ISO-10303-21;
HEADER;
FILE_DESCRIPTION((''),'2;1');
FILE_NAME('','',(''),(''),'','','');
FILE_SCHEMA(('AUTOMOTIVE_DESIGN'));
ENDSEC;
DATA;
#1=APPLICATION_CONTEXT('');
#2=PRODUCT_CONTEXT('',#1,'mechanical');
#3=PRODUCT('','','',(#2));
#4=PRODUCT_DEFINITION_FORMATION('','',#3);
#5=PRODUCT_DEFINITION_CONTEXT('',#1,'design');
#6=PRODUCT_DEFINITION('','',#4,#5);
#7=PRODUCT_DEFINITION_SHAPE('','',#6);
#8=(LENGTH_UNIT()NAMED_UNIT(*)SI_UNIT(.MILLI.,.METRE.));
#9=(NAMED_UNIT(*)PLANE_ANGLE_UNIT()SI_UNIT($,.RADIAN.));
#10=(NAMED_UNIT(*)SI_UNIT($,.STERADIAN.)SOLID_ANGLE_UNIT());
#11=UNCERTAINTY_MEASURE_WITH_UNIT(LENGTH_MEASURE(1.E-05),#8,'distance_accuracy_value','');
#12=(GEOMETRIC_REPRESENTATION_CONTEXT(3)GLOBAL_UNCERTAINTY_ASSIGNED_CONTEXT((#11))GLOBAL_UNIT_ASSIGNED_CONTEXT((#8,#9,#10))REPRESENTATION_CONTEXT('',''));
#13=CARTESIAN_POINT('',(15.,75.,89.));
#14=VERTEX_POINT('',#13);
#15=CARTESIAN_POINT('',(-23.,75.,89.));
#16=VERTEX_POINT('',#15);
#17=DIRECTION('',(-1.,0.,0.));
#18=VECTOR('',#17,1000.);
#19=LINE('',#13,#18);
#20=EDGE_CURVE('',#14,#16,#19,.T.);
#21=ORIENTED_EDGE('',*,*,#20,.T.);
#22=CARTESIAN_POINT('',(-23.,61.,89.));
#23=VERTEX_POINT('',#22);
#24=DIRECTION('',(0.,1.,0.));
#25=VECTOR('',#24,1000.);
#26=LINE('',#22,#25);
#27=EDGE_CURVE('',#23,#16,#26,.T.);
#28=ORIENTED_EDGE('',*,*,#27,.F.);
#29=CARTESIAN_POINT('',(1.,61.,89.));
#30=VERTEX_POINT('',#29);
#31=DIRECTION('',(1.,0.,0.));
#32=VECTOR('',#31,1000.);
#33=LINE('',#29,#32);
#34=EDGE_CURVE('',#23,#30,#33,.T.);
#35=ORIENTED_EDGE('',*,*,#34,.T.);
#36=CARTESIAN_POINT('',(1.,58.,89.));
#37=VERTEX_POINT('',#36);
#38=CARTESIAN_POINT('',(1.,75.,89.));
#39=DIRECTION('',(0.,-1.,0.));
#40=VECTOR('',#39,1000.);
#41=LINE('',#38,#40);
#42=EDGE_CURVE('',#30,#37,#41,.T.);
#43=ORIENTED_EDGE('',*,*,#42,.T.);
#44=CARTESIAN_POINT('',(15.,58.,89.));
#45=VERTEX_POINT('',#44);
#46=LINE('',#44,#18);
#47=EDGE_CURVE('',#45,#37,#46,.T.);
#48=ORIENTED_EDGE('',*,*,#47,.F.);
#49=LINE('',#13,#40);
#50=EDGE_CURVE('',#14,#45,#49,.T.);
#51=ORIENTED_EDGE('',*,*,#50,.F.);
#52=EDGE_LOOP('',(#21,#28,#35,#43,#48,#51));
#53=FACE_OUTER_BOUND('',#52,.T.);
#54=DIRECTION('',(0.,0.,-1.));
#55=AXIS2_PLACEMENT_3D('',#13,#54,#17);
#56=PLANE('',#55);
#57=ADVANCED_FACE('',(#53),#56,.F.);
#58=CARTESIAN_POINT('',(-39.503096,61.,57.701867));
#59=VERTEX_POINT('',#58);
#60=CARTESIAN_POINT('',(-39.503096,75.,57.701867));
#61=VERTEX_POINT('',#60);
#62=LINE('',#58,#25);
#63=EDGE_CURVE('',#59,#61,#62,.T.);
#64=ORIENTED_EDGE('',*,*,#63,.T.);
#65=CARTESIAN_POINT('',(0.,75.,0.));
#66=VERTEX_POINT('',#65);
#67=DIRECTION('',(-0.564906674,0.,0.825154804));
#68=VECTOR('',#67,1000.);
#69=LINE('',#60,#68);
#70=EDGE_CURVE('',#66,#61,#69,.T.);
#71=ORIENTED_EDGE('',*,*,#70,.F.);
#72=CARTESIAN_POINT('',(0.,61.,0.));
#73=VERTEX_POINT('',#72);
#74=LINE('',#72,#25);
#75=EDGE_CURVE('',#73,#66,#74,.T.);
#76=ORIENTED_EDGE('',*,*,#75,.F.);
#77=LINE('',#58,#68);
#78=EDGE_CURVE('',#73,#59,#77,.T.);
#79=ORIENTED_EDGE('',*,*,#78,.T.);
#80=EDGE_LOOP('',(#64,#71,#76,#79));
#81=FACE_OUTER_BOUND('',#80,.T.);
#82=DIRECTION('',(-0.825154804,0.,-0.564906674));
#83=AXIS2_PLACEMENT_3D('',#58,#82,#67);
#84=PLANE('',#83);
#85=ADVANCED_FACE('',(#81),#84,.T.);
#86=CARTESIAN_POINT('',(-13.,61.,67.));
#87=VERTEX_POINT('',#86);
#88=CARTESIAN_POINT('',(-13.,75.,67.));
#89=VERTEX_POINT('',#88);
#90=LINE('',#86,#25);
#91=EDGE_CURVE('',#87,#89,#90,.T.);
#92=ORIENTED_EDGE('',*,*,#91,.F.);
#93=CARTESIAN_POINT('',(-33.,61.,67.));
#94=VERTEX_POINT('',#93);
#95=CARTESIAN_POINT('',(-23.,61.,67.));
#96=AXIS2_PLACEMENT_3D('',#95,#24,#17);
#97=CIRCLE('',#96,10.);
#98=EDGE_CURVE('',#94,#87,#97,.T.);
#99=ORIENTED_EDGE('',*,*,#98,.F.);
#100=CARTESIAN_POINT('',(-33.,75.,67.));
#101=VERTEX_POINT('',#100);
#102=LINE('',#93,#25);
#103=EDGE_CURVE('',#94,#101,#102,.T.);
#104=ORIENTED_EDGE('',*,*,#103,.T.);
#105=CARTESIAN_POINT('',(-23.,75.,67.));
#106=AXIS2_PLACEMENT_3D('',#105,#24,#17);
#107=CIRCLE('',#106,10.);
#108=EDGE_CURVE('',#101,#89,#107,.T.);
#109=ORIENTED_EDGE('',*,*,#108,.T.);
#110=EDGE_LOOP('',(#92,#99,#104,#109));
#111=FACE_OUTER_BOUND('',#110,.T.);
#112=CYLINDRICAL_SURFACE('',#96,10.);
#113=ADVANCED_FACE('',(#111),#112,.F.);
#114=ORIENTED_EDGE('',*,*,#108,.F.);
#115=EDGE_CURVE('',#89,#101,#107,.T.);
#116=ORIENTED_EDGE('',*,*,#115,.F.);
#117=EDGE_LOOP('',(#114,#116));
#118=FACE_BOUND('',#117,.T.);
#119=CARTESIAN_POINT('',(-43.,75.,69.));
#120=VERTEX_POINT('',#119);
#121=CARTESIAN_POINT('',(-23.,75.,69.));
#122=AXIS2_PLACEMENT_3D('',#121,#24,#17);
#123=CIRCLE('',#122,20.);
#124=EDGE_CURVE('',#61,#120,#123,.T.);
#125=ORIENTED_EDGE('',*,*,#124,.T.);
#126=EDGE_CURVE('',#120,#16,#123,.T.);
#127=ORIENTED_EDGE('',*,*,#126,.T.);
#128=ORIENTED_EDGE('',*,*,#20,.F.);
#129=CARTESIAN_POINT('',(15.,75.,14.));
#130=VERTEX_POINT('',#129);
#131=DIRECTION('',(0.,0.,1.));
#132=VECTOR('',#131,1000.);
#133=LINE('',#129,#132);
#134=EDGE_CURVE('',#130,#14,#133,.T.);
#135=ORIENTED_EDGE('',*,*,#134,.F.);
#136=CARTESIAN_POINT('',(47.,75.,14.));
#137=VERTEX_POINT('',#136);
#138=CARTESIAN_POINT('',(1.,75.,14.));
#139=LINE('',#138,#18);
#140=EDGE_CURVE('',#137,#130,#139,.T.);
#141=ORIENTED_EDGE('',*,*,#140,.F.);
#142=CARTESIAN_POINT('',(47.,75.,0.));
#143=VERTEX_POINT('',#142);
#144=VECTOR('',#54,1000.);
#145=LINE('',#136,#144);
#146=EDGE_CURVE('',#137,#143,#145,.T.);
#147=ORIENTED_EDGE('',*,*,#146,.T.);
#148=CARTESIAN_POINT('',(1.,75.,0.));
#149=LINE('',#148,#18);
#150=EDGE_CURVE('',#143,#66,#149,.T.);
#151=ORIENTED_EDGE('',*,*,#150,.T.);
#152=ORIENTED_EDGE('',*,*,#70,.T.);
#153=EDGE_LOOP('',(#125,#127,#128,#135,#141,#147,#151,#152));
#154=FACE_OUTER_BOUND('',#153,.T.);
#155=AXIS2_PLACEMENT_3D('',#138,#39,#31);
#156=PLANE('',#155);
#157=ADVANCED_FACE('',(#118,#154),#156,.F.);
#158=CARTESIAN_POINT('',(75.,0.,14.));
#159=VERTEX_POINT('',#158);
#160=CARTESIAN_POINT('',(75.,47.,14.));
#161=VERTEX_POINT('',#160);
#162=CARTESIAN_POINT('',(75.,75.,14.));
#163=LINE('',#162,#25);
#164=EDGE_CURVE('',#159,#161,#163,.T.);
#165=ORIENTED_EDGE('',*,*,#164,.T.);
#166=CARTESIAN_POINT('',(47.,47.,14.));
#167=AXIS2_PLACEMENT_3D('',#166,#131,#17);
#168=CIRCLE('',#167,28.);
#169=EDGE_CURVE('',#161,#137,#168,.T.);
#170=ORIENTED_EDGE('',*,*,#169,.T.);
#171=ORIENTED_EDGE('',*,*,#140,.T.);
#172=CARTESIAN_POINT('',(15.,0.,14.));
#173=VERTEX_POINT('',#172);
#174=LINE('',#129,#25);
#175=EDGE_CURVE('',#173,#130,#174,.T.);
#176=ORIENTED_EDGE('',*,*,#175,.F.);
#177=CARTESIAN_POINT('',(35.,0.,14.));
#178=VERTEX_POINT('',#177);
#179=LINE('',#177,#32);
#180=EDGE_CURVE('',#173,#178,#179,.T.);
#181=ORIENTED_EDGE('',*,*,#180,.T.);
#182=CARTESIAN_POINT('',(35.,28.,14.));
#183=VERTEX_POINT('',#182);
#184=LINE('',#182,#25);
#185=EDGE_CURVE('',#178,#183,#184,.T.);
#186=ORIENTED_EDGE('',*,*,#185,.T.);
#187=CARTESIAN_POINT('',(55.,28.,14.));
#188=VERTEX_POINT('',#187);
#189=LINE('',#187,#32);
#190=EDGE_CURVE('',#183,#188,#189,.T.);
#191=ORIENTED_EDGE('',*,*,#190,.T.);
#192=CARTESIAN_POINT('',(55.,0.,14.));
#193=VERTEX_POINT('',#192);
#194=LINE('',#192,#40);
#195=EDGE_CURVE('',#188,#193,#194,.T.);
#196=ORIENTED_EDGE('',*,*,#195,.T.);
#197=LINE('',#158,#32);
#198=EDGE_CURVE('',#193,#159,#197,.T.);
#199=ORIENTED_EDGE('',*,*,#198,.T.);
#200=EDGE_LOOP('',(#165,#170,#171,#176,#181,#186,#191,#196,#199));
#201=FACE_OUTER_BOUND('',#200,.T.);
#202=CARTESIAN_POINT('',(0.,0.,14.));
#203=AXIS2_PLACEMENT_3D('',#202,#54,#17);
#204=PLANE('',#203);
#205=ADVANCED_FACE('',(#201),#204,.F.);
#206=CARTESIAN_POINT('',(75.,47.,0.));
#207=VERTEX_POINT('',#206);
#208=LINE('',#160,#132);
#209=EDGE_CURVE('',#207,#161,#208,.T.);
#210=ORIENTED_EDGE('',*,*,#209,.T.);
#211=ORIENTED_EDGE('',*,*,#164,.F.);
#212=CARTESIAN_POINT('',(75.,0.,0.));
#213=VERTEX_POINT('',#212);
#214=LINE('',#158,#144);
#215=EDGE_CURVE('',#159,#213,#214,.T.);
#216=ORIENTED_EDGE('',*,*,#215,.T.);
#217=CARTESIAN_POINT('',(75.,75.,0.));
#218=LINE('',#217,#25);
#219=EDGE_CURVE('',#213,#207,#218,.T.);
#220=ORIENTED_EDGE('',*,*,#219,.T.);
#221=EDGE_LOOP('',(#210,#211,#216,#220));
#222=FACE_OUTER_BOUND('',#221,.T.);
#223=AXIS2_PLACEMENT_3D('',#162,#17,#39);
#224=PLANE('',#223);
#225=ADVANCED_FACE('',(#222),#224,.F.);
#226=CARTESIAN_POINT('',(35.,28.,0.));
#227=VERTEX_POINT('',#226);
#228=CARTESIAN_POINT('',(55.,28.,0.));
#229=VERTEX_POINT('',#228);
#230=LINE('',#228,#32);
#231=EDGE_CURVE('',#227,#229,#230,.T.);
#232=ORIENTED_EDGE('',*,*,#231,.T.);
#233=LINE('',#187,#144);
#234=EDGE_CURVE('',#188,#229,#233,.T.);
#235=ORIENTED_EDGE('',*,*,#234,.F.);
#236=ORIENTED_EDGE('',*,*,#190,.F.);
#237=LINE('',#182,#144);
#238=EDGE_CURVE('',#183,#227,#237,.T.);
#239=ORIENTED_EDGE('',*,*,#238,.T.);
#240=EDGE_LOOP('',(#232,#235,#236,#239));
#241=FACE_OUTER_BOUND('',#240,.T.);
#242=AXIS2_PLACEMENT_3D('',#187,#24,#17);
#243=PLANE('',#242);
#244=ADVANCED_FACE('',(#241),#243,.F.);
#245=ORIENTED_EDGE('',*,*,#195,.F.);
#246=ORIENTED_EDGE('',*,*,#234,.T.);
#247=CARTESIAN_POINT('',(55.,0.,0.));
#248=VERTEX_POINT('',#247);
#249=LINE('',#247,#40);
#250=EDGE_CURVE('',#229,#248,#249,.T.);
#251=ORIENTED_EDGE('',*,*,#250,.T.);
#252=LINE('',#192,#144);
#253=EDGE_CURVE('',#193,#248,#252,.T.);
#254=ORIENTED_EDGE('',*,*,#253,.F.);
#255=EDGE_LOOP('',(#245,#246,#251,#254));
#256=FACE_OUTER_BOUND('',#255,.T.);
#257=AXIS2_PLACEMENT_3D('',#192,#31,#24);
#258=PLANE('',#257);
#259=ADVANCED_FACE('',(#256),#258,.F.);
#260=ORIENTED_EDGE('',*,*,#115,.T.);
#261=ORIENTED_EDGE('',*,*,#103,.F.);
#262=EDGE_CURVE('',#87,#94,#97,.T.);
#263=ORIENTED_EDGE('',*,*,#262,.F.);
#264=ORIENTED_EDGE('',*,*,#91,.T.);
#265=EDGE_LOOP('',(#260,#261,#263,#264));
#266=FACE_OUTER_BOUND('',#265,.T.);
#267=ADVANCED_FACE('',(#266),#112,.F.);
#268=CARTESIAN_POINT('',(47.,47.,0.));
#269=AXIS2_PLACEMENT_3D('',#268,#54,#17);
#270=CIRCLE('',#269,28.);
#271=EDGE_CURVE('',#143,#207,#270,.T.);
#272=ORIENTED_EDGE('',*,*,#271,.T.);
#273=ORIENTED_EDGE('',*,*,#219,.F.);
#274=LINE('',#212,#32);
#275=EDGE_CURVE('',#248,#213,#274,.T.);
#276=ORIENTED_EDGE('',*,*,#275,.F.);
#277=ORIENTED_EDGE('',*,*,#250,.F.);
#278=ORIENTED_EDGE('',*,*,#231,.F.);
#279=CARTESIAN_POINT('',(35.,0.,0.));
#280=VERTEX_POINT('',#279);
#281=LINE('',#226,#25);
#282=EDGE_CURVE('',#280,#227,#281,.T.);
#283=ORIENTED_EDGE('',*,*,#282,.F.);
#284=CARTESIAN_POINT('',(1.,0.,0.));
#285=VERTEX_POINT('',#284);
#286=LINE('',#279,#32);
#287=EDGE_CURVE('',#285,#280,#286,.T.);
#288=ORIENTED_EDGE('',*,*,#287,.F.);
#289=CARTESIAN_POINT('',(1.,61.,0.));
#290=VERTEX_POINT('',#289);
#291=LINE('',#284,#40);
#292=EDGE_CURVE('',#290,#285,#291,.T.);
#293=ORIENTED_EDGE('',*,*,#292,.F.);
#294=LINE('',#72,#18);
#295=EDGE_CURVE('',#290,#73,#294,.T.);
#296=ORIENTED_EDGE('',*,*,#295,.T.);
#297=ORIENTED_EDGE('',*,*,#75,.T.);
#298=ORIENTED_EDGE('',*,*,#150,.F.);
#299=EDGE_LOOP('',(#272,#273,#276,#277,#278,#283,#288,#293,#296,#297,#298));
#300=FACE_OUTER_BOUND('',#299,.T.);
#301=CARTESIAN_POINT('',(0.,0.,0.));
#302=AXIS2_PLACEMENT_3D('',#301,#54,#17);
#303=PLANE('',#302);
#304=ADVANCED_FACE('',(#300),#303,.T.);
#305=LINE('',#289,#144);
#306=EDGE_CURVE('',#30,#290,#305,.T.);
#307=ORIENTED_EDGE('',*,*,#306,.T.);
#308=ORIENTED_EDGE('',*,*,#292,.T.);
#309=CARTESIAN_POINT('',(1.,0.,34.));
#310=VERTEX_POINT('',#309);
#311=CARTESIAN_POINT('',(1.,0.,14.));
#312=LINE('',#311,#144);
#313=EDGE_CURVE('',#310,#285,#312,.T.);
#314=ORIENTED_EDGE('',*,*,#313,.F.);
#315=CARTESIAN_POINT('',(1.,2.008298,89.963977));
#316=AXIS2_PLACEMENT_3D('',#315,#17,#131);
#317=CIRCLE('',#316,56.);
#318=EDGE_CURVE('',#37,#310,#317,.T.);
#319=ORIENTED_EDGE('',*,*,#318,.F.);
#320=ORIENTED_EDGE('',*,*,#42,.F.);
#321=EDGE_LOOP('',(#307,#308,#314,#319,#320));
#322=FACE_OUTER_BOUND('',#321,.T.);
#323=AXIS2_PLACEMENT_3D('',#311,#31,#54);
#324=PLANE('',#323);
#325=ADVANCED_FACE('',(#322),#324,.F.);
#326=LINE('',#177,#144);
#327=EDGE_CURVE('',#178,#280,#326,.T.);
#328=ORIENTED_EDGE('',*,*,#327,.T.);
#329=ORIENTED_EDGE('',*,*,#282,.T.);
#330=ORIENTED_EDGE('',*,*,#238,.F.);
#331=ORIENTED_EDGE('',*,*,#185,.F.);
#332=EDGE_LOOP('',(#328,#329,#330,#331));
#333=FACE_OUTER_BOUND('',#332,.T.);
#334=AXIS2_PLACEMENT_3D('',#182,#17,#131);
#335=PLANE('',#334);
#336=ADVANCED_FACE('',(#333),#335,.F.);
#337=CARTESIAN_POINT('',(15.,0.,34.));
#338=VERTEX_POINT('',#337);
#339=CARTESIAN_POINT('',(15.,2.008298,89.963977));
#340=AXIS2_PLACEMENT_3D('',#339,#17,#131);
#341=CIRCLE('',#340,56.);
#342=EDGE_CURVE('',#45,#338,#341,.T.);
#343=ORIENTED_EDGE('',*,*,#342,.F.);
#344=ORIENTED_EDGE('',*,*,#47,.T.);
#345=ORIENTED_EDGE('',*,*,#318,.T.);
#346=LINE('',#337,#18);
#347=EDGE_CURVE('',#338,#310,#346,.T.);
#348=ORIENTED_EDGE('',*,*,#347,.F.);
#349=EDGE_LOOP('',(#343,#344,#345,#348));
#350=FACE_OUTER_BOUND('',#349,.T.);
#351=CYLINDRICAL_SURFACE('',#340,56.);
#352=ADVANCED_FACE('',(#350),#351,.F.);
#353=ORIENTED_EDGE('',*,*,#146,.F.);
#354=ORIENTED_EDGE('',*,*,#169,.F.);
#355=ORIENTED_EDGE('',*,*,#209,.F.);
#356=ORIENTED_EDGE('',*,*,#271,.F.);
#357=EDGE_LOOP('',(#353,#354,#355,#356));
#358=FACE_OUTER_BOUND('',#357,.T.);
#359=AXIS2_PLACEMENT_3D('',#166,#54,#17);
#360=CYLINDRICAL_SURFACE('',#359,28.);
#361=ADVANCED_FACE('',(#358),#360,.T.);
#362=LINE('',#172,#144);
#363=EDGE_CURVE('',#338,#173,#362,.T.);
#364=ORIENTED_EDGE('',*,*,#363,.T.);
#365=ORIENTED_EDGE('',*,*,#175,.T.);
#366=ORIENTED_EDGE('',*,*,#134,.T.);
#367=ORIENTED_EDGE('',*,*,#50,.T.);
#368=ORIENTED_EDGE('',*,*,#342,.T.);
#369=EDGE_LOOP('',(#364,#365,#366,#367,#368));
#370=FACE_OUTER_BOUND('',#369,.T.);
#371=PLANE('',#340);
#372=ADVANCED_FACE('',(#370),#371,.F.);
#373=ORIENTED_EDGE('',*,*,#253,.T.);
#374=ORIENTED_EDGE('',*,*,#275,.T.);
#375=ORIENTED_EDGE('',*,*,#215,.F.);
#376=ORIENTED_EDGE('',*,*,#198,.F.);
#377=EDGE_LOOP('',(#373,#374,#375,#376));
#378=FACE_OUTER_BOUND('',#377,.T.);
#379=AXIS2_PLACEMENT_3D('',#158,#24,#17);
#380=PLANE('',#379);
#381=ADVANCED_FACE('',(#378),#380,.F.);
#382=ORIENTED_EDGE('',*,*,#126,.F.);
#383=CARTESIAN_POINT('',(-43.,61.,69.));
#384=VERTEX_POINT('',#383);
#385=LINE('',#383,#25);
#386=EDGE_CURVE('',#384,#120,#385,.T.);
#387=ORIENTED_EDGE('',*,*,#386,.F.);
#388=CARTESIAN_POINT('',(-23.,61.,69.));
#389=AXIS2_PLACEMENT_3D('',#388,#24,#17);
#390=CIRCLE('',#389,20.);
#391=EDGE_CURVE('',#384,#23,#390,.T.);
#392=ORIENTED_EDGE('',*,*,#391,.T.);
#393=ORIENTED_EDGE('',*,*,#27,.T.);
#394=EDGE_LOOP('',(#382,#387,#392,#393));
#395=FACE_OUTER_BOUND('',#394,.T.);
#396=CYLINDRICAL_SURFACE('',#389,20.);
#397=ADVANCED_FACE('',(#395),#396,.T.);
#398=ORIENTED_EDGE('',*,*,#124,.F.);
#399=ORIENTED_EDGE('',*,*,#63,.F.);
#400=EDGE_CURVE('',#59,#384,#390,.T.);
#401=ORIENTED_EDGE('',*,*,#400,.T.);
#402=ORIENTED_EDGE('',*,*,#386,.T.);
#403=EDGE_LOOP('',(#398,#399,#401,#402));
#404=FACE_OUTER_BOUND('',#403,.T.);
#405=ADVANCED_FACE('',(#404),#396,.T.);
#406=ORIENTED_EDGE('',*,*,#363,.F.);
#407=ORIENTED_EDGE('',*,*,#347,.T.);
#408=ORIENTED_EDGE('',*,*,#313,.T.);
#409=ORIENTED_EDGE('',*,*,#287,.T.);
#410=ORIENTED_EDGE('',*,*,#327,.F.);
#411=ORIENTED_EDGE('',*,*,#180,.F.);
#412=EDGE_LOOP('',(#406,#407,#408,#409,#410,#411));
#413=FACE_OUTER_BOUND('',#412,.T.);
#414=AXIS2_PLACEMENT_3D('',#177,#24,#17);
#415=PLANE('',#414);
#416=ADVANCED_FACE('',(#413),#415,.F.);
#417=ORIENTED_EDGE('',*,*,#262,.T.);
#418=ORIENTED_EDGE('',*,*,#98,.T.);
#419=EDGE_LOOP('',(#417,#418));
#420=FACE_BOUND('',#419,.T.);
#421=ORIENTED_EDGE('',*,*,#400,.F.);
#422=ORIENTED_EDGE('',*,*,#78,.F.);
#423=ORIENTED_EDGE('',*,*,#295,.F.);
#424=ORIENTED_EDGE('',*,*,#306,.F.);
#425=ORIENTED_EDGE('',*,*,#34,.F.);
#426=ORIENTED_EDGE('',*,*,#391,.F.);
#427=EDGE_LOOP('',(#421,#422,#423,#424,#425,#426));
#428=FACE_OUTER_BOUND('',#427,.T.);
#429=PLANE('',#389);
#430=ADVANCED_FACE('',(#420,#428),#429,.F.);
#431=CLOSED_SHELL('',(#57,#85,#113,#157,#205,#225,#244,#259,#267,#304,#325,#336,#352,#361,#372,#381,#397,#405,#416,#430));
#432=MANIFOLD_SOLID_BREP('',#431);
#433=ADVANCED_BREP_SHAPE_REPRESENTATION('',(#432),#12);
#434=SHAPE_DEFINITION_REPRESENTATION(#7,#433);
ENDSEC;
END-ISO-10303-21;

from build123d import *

# Parameters (mm, degrees)
BASE_PLATE_14MM_DEPTH  = 14
UPRIGHT_START          = 1
UPRIGHT_WEB_14MM_DEPTH = 14
SIDE_LUG_SKETCH_R      = 10
SIDE_LUG_14MM_DEPTH    = 14
CORNER_ROUND_R28_R     = 28


with BuildPart() as part:
    # Base Plate Sketch → Base Plate 14mm (new body)
    with BuildSketch(Plane.XY):
        Polygon((1, 0), (1, 75), (75, 75), (75, 0), (55, 0), (55, 28), (35, 28), (35, 0), align=None)
    extrude(amount=BASE_PLATE_14MM_DEPTH)

    # Upright Web Sketch → Upright Web 14mm (add)
    with BuildSketch(Plane(origin=(0, 0, 0), x_dir=(0, 0, -1), z_dir=(1, 0, 0)).offset(UPRIGHT_START)):
        with BuildLine():
            Line((-14, 75), (-89, 75))
            Line((-89, 75), (-89, 58))
            ThreePointArc((-89, 58), (-49.329041508, 40.541426156), (-34, 0))
            Line((-34, 0), (-14, 0))
            Line((-14, 0), (-14, 75))
        make_face()
    extrude(amount=UPRIGHT_WEB_14MM_DEPTH)

    # Side Lug Sketch → Side Lug 14mm (add)
    with BuildSketch(Plane(origin=(0, 75, 0), x_dir=(1, 0, 0), z_dir=(0, 1, 0))):
        with BuildLine():
            Line((1, -89), (-23, -89))
            ThreePointArc((-23, -89), (-40.691278494, -78.328379563), (-39.503096073, -57.701866526))
            Line((-39.503096073, -57.701866526), (0, 0))
            Line((0, 0), (1, 0))
            Line((1, 0), (1, -89))
        make_face()
        with Locations(Location((-23, -67, 0), (0, 0, 180))):
            Circle(SIDE_LUG_SKETCH_R, mode=Mode.SUBTRACT)
    extrude(amount=-SIDE_LUG_14MM_DEPTH)

    # Corner Round R28
    corner_round_r28_edges = [part.edges().sort_by_distance(p)[0] for p in [
        (75, 75, 7),
    ]]
    fillet(corner_round_r28_edges, radius=CORNER_ROUND_R28_R)


solid = part.part
